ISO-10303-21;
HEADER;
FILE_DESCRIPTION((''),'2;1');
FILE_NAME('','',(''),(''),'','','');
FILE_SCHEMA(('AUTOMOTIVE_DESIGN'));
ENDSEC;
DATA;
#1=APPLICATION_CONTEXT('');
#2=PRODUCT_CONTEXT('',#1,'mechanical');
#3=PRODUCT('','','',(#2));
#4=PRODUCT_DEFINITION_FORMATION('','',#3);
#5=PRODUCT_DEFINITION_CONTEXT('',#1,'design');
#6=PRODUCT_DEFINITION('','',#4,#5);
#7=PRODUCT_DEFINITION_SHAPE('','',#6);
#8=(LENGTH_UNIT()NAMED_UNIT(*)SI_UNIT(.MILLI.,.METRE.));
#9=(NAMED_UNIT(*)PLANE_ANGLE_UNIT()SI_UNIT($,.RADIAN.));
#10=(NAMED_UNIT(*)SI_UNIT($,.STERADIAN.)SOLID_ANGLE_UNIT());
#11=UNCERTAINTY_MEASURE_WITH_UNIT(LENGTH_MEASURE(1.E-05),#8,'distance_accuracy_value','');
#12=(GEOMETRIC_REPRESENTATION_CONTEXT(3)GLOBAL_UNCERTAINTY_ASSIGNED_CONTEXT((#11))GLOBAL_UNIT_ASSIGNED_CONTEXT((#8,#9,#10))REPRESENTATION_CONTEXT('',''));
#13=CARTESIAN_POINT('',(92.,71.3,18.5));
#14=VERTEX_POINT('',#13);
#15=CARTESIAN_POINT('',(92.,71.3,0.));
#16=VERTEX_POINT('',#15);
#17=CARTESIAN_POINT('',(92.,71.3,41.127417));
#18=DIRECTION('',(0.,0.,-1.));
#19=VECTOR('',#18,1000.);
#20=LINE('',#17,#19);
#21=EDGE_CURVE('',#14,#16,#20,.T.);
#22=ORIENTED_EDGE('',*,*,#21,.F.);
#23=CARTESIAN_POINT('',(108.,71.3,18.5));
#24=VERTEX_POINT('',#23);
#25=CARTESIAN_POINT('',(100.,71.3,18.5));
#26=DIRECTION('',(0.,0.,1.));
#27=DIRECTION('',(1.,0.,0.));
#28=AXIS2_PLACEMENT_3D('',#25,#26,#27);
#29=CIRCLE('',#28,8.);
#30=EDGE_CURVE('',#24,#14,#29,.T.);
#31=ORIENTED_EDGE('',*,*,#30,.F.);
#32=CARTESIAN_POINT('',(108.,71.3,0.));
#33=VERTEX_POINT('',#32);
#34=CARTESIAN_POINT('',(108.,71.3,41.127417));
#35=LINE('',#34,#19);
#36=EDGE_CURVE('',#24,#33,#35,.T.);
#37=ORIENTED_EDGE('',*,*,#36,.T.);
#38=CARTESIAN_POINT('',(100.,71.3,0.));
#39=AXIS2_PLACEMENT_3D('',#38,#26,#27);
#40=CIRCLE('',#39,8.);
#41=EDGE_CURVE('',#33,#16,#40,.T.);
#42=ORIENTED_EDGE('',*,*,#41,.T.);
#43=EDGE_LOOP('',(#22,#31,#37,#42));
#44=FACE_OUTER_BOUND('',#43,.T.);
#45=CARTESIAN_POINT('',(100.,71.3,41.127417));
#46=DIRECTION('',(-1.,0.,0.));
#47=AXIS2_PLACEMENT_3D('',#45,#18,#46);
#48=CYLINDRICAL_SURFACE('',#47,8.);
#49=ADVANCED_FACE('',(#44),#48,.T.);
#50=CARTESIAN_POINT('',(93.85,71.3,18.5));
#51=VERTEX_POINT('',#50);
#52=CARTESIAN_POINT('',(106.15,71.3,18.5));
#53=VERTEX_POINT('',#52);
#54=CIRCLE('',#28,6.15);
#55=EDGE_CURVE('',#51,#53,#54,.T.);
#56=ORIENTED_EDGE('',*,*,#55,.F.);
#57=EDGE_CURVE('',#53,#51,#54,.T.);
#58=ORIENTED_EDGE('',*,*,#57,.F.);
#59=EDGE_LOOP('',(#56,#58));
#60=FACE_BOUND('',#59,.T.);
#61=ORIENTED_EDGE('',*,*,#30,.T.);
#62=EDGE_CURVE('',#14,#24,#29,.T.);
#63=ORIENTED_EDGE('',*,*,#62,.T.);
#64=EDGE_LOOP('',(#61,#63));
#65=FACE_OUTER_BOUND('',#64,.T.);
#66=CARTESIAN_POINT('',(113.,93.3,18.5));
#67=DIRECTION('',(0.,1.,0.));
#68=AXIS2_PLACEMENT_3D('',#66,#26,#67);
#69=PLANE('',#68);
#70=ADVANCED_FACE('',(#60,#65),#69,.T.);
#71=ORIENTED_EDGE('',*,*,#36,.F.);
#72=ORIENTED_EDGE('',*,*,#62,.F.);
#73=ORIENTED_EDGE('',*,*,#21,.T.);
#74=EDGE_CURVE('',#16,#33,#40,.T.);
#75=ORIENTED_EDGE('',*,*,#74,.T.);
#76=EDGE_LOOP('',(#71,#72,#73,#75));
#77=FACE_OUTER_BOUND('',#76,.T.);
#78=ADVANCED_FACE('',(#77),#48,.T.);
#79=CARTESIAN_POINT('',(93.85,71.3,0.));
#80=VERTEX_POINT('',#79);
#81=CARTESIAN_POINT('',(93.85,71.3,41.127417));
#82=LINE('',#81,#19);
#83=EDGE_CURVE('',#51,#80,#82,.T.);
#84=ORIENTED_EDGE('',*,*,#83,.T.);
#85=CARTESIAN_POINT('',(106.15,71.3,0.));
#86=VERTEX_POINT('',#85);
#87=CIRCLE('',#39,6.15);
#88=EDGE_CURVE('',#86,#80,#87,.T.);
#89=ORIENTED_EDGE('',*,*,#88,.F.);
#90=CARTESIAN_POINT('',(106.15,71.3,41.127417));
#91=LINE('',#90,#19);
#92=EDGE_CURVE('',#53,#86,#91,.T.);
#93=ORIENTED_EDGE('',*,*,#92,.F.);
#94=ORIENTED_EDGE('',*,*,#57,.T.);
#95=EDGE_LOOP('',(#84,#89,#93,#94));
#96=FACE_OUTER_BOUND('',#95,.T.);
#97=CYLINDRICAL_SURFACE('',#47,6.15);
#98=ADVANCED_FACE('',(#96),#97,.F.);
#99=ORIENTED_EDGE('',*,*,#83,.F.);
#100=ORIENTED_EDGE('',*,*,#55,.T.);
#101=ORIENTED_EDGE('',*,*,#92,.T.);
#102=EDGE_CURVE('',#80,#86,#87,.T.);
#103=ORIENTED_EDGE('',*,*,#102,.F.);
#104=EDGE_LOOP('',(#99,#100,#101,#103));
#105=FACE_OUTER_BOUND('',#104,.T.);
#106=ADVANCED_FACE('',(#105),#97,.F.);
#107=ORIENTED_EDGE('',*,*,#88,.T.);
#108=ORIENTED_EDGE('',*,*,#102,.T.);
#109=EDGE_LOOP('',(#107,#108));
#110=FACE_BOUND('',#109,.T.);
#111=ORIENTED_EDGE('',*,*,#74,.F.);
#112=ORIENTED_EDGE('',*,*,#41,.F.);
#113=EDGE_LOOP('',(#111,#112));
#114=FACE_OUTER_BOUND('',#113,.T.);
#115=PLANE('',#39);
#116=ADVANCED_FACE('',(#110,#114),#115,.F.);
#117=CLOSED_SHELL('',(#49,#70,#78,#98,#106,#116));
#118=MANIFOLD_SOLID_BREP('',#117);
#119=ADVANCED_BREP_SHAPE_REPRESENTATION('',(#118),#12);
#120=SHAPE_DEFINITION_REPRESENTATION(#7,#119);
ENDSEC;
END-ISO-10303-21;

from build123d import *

# Parameters (mm, degrees)
SKETCH1_R           = 8
SKETCH1_R_2         = 6.15
BOSS_EXTRUDE1_DEPTH = 18.5


with BuildPart() as part:
    # Sketch1 → Boss-Extrude1 (new body)
    with BuildSketch(Plane.XY):
        with Locations((100, 71.3)):
            Circle(SKETCH1_R)
        with Locations((100, 71.3)):
            Circle(SKETCH1_R_2, mode=Mode.SUBTRACT)
    extrude(amount=BOSS_EXTRUDE1_DEPTH)


solid = part.part
